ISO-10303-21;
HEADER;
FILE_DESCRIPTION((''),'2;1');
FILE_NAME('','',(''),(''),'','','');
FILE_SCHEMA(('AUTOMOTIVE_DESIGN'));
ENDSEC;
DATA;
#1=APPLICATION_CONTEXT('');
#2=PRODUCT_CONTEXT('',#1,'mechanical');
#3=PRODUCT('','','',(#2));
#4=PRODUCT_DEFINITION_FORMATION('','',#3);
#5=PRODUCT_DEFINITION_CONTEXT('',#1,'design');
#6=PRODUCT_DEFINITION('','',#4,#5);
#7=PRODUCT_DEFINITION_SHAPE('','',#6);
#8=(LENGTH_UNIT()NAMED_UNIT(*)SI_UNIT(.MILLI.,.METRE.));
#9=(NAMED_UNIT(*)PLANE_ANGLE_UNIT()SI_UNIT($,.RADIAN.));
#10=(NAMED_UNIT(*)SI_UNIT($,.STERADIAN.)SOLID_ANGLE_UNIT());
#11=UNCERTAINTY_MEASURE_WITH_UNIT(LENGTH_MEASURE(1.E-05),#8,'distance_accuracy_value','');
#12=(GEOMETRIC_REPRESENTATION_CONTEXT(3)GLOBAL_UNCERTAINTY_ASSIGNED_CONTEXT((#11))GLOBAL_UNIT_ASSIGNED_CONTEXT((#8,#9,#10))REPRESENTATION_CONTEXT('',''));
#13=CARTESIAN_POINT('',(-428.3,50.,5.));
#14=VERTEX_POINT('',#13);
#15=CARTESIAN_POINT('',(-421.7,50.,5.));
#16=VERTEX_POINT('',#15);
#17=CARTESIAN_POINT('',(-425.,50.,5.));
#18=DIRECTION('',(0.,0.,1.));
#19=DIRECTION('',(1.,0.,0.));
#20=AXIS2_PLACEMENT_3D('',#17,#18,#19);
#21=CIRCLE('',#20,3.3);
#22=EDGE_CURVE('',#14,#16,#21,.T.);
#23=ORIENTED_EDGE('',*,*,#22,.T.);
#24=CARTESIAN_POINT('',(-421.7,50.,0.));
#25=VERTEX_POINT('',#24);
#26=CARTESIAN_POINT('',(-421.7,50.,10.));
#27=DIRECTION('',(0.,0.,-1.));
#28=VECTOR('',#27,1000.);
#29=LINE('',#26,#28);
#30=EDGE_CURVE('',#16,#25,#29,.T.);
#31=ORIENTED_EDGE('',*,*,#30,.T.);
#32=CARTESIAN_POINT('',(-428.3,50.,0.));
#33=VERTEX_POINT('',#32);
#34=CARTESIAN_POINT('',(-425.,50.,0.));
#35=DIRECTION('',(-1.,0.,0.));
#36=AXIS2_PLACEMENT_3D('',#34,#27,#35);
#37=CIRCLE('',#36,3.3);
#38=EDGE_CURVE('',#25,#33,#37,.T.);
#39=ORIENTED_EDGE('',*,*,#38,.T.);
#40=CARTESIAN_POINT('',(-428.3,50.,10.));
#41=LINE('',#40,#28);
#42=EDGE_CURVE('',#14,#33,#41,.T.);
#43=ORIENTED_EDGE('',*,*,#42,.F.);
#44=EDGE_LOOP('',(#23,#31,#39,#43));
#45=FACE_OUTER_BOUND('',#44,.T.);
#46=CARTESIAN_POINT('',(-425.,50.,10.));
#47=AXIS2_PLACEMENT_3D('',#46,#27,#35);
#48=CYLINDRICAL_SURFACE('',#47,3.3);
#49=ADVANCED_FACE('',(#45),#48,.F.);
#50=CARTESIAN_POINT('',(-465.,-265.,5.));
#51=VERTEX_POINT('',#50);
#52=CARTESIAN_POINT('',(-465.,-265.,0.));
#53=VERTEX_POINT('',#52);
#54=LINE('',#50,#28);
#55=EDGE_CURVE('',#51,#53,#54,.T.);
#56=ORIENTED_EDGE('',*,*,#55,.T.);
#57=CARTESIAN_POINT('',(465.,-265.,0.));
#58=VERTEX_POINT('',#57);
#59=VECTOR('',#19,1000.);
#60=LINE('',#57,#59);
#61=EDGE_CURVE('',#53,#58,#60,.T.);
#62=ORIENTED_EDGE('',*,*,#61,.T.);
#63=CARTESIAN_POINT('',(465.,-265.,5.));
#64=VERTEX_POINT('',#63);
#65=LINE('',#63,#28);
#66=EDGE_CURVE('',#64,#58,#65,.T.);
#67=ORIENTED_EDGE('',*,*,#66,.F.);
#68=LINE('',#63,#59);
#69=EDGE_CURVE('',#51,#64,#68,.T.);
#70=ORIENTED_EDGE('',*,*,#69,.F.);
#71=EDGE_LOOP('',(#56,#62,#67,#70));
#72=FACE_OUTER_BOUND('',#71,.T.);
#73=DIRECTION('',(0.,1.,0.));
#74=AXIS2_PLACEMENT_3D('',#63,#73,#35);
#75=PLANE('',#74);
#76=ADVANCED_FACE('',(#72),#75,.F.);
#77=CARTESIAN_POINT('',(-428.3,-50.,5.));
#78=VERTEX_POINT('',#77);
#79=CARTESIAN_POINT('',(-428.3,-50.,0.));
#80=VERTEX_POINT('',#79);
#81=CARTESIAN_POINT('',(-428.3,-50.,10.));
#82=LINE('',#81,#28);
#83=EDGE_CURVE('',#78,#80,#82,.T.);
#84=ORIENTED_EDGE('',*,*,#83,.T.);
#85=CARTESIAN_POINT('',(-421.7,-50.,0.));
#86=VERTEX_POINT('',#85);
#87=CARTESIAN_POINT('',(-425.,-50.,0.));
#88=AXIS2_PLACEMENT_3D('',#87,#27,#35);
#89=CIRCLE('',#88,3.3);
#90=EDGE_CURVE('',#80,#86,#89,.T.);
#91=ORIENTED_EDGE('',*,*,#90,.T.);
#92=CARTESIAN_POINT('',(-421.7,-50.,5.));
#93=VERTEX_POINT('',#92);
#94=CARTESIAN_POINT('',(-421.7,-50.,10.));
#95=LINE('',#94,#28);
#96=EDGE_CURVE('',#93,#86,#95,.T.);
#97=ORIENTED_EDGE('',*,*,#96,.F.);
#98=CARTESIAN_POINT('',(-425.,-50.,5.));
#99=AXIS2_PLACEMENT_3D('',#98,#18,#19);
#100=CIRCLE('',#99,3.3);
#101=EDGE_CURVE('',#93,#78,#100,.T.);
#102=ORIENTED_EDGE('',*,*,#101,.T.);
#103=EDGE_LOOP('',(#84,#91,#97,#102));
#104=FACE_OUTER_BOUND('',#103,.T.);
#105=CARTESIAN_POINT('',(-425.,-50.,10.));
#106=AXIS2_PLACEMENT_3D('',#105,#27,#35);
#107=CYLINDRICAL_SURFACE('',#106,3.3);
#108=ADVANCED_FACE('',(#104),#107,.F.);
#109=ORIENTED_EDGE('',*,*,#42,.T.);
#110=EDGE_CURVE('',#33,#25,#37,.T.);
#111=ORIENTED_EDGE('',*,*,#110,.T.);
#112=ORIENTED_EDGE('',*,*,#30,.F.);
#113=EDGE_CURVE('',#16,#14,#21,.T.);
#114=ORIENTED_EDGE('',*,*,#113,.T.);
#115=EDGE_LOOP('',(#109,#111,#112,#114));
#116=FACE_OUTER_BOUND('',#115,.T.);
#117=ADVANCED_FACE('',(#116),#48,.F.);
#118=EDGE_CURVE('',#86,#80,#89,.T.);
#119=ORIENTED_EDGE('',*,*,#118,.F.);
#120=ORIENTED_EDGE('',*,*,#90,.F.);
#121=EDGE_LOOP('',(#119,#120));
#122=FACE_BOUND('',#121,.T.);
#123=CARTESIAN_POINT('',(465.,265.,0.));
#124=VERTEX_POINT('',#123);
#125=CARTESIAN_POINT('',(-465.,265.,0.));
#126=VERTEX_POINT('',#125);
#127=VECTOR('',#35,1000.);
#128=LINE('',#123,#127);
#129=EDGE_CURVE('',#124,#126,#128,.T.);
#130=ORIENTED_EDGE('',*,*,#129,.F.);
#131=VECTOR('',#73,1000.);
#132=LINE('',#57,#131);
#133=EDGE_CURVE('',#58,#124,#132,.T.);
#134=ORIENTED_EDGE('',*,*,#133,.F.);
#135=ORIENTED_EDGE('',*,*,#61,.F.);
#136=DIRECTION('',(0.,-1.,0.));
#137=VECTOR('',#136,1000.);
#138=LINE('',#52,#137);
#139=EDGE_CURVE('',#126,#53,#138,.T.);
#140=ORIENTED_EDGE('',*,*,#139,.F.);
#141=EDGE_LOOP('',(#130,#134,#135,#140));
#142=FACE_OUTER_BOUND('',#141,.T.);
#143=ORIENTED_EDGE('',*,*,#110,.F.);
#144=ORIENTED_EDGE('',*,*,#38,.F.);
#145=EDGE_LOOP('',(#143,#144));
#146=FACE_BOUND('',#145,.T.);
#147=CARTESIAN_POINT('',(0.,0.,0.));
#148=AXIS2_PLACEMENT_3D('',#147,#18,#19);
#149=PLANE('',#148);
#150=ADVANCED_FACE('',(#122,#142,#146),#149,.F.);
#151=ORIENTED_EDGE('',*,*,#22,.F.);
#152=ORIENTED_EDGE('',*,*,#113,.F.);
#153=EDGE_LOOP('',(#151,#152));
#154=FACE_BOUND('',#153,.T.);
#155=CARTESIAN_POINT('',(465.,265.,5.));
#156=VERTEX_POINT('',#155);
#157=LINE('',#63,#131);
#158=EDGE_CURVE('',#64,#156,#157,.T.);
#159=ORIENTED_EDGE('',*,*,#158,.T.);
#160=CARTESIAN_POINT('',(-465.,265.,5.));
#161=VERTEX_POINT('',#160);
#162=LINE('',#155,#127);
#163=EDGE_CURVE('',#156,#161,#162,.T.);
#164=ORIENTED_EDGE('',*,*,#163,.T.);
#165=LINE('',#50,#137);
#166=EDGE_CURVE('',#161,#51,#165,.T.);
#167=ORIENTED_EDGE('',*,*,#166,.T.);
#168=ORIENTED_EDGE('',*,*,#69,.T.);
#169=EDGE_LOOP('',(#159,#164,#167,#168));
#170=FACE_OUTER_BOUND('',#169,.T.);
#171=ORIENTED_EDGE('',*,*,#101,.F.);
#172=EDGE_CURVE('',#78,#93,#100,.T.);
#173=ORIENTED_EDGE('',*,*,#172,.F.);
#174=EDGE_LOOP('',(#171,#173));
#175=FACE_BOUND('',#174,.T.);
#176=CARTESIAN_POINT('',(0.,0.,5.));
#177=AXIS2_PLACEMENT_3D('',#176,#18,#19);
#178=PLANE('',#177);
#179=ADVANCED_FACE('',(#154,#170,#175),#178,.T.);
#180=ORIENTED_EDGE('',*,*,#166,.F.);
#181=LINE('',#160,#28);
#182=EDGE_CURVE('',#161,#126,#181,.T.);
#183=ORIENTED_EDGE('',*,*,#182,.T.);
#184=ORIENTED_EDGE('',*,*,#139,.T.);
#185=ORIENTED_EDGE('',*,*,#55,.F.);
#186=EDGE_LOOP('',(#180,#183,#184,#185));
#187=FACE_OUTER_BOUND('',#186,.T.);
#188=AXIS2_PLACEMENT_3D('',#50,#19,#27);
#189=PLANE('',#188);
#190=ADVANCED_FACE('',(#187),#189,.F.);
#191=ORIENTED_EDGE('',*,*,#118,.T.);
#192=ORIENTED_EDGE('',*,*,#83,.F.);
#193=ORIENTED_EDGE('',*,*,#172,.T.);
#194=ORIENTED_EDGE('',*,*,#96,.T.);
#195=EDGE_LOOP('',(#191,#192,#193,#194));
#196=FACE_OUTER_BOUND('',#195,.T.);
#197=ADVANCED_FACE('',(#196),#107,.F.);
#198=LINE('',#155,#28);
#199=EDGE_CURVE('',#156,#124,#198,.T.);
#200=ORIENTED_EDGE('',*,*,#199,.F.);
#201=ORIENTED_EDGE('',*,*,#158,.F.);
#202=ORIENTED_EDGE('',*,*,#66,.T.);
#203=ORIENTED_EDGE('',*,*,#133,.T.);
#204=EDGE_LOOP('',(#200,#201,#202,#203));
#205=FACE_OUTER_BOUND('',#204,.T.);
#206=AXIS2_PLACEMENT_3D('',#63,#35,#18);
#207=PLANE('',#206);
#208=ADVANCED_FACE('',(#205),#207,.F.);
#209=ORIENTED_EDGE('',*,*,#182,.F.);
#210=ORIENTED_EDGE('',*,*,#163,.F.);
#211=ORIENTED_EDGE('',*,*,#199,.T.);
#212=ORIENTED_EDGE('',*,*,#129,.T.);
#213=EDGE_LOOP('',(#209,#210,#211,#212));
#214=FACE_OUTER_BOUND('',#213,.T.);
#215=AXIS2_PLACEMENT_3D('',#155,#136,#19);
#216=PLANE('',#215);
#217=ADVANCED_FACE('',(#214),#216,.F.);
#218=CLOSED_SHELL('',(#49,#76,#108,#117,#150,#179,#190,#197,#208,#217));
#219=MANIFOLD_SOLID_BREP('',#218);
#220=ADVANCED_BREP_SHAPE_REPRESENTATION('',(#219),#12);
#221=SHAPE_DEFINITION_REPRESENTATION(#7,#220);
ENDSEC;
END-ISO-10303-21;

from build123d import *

# Parameters (mm, degrees)
SKETCH_1_W          = 930
SKETCH_1_H          = 530
EXTRUDE_1_DEPTH     = 5
SKETCH_2_R          = 3.3
CUT_EXTRUDE_1_DEPTH = 10


with BuildPart() as part:
    # 草图1 → 凸台-拉伸1 (new body)
    with BuildSketch(Plane.XY):
        Rectangle(SKETCH_1_W, SKETCH_1_H)
    extrude(amount=EXTRUDE_1_DEPTH)

    # 草图2 → 切除-拉伸1 (cut)
    with BuildSketch(Plane(origin=(0, 0, 0), x_dir=(-1, 0, 0), z_dir=(0, 0, -1))):
        with Locations((425, 50)):
            Circle(SKETCH_2_R)
        with Locations((425, -50)):
            Circle(SKETCH_2_R)
    extrude(amount=-CUT_EXTRUDE_1_DEPTH, mode=Mode.SUBTRACT)


solid = part.part
